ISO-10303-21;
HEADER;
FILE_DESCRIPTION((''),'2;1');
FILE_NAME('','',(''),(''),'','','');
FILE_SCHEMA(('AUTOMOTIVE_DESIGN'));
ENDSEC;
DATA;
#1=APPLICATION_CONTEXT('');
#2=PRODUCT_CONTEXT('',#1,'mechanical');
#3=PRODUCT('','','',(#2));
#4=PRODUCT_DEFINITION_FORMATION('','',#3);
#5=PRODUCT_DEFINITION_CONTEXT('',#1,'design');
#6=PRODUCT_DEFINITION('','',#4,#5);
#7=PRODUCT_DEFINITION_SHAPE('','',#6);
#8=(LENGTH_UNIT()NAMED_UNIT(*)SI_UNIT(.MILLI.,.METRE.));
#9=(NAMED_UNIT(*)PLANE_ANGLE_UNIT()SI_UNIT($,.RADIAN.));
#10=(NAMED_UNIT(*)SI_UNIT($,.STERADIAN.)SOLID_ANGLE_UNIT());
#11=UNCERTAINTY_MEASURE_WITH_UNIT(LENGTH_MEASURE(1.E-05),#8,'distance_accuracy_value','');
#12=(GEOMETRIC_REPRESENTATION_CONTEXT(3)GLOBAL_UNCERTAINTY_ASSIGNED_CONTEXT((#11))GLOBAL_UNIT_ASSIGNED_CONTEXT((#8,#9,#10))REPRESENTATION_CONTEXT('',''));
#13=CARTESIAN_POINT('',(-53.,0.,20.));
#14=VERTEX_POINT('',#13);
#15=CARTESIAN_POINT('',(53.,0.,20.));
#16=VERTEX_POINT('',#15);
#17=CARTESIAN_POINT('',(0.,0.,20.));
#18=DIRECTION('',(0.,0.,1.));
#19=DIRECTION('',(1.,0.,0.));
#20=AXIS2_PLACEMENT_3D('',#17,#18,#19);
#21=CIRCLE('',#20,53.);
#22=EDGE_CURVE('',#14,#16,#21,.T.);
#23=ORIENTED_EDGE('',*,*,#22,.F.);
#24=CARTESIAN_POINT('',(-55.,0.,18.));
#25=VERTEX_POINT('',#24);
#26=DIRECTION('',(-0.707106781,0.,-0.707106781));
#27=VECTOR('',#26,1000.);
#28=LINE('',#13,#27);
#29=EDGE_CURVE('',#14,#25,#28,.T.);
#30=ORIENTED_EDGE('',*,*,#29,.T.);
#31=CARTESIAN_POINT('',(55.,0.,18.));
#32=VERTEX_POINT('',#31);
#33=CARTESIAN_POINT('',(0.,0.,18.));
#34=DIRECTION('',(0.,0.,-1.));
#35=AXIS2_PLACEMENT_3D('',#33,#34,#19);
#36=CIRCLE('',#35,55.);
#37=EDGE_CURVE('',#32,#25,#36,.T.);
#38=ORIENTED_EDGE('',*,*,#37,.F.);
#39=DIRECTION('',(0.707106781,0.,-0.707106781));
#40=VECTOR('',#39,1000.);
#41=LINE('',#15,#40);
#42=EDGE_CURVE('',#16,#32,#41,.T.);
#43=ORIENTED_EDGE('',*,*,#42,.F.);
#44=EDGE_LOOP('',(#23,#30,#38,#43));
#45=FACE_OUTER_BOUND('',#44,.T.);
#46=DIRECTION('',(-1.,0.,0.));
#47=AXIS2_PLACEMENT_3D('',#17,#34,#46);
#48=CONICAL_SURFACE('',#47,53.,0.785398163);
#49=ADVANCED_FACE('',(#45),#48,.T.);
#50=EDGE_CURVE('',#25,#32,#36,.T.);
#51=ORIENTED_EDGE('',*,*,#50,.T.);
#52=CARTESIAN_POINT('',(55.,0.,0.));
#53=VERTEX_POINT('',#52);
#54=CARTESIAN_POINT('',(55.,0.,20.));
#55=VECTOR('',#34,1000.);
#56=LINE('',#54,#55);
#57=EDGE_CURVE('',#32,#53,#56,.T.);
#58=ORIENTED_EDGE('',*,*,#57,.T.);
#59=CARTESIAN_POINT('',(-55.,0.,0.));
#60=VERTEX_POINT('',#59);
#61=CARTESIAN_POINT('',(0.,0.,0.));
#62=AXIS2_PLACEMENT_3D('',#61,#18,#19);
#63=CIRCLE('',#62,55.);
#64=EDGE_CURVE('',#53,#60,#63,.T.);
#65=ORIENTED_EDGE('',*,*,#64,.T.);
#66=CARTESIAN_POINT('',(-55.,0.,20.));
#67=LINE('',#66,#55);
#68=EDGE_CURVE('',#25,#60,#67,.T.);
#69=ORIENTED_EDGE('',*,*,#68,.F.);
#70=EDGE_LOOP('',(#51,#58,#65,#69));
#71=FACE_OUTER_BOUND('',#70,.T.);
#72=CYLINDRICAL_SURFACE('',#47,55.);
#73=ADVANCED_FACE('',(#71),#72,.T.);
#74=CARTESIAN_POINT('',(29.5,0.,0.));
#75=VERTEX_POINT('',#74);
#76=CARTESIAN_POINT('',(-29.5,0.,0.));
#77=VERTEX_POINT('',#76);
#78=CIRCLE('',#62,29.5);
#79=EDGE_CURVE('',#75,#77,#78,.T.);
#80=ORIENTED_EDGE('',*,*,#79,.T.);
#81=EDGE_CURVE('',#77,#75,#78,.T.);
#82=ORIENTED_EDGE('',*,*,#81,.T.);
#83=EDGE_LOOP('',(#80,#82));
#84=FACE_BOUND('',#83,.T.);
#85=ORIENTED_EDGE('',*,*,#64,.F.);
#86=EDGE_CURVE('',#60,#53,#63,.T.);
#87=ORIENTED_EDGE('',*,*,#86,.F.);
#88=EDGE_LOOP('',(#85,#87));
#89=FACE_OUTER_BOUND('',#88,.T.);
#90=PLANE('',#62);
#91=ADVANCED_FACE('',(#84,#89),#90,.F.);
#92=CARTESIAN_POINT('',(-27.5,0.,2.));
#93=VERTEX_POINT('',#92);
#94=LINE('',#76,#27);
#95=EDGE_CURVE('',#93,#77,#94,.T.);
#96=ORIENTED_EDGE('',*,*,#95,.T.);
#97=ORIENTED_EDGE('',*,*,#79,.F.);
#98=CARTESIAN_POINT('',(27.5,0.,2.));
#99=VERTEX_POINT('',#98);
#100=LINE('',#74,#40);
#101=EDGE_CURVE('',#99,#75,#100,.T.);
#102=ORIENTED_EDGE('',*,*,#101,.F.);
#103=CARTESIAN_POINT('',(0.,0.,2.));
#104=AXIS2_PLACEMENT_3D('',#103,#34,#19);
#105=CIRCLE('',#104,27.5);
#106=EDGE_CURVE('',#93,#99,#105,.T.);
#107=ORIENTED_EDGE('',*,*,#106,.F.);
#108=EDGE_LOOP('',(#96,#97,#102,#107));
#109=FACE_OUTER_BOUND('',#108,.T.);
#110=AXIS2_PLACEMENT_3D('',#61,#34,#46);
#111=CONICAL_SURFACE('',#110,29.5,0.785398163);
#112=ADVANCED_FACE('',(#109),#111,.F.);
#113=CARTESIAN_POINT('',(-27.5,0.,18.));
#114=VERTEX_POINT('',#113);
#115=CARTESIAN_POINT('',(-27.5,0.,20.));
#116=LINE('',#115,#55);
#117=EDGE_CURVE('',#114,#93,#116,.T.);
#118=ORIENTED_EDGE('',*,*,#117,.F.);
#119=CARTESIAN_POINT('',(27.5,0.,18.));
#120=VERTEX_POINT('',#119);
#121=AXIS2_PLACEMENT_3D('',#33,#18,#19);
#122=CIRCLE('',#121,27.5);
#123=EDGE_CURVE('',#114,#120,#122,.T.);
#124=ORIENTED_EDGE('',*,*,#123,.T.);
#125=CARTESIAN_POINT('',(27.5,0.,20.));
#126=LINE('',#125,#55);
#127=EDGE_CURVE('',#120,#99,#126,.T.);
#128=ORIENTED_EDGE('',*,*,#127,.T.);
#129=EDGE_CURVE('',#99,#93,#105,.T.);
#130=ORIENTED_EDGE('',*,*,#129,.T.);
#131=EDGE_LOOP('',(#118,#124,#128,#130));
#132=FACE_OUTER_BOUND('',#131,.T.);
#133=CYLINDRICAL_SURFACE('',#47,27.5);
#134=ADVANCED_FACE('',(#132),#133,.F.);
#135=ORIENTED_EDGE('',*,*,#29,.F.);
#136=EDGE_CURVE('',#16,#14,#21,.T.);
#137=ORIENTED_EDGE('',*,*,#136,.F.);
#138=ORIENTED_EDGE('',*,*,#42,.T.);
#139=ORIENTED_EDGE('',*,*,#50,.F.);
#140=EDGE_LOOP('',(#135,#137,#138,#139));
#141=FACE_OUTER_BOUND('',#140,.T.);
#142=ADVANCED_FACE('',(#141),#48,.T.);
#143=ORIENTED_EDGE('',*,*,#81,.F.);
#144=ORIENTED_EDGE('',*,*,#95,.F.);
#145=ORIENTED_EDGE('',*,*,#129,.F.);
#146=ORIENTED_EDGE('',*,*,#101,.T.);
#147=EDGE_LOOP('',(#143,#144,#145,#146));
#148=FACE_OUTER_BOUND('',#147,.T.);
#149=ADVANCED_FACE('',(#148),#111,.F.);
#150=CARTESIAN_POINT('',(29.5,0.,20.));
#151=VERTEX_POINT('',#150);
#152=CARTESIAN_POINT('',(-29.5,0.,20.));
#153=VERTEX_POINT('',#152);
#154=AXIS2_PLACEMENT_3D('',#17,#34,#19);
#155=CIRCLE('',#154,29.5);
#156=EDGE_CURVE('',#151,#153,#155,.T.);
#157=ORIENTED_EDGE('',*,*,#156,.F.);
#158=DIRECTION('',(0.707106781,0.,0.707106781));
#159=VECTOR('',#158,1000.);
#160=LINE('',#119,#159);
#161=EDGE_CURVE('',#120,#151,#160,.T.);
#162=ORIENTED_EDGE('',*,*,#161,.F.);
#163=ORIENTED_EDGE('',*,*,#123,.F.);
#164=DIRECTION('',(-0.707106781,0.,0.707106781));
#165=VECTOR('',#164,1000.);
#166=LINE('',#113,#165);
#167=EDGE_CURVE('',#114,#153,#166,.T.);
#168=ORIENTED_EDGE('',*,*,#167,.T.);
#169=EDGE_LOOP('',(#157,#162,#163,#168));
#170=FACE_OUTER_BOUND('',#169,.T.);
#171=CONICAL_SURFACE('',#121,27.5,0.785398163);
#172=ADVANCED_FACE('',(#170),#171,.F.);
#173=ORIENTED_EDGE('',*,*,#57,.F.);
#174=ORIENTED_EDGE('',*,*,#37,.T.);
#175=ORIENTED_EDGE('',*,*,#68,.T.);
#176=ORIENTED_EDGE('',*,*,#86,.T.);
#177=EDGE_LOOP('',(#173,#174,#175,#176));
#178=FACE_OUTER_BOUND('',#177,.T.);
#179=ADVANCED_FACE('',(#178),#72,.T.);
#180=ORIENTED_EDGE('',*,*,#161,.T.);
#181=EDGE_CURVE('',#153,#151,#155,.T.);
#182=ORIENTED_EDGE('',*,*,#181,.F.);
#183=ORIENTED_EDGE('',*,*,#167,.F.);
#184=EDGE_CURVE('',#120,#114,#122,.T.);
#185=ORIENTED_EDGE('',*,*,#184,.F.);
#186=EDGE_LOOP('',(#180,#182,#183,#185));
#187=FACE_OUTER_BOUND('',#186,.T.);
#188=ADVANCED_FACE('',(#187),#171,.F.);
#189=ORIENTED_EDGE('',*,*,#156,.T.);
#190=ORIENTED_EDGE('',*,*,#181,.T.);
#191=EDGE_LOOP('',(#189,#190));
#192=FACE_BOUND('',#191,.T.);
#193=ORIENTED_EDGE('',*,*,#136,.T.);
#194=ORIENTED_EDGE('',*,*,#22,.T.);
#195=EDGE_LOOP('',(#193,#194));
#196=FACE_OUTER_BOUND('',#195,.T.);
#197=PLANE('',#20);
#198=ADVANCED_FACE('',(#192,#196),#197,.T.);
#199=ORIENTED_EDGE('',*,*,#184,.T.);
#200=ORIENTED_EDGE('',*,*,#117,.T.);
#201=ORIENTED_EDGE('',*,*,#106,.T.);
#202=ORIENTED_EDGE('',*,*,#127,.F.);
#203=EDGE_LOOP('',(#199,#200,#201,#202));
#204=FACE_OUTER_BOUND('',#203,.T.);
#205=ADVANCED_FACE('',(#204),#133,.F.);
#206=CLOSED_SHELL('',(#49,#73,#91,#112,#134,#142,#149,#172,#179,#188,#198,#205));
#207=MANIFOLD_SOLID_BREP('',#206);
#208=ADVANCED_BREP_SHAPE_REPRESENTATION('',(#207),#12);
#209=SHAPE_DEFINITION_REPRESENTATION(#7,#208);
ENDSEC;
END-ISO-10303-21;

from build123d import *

# Parameters (mm, degrees)
SKETCH1_R           = 55
SKETCH1_R_2         = 27.5
BOSS_EXTRUDE1_DEPTH = 20
CHAMFER1_SIZE       = 2


with BuildPart() as part:
    # Sketch1 → Boss-Extrude1 (new body)
    with BuildSketch(Plane.XY):
        Circle(SKETCH1_R)
        Circle(SKETCH1_R_2, mode=Mode.SUBTRACT)
    extrude(amount=BOSS_EXTRUDE1_DEPTH)

    # Chamfer1
    chamfer1_edges = [part.edges().sort_by_distance(p)[0] for p in [
        (-55, 0, 20),
        (-27.5, 0, 0),
        (-27.5, 0, 20),
    ]]
    chamfer(chamfer1_edges, length=CHAMFER1_SIZE)


solid = part.part
